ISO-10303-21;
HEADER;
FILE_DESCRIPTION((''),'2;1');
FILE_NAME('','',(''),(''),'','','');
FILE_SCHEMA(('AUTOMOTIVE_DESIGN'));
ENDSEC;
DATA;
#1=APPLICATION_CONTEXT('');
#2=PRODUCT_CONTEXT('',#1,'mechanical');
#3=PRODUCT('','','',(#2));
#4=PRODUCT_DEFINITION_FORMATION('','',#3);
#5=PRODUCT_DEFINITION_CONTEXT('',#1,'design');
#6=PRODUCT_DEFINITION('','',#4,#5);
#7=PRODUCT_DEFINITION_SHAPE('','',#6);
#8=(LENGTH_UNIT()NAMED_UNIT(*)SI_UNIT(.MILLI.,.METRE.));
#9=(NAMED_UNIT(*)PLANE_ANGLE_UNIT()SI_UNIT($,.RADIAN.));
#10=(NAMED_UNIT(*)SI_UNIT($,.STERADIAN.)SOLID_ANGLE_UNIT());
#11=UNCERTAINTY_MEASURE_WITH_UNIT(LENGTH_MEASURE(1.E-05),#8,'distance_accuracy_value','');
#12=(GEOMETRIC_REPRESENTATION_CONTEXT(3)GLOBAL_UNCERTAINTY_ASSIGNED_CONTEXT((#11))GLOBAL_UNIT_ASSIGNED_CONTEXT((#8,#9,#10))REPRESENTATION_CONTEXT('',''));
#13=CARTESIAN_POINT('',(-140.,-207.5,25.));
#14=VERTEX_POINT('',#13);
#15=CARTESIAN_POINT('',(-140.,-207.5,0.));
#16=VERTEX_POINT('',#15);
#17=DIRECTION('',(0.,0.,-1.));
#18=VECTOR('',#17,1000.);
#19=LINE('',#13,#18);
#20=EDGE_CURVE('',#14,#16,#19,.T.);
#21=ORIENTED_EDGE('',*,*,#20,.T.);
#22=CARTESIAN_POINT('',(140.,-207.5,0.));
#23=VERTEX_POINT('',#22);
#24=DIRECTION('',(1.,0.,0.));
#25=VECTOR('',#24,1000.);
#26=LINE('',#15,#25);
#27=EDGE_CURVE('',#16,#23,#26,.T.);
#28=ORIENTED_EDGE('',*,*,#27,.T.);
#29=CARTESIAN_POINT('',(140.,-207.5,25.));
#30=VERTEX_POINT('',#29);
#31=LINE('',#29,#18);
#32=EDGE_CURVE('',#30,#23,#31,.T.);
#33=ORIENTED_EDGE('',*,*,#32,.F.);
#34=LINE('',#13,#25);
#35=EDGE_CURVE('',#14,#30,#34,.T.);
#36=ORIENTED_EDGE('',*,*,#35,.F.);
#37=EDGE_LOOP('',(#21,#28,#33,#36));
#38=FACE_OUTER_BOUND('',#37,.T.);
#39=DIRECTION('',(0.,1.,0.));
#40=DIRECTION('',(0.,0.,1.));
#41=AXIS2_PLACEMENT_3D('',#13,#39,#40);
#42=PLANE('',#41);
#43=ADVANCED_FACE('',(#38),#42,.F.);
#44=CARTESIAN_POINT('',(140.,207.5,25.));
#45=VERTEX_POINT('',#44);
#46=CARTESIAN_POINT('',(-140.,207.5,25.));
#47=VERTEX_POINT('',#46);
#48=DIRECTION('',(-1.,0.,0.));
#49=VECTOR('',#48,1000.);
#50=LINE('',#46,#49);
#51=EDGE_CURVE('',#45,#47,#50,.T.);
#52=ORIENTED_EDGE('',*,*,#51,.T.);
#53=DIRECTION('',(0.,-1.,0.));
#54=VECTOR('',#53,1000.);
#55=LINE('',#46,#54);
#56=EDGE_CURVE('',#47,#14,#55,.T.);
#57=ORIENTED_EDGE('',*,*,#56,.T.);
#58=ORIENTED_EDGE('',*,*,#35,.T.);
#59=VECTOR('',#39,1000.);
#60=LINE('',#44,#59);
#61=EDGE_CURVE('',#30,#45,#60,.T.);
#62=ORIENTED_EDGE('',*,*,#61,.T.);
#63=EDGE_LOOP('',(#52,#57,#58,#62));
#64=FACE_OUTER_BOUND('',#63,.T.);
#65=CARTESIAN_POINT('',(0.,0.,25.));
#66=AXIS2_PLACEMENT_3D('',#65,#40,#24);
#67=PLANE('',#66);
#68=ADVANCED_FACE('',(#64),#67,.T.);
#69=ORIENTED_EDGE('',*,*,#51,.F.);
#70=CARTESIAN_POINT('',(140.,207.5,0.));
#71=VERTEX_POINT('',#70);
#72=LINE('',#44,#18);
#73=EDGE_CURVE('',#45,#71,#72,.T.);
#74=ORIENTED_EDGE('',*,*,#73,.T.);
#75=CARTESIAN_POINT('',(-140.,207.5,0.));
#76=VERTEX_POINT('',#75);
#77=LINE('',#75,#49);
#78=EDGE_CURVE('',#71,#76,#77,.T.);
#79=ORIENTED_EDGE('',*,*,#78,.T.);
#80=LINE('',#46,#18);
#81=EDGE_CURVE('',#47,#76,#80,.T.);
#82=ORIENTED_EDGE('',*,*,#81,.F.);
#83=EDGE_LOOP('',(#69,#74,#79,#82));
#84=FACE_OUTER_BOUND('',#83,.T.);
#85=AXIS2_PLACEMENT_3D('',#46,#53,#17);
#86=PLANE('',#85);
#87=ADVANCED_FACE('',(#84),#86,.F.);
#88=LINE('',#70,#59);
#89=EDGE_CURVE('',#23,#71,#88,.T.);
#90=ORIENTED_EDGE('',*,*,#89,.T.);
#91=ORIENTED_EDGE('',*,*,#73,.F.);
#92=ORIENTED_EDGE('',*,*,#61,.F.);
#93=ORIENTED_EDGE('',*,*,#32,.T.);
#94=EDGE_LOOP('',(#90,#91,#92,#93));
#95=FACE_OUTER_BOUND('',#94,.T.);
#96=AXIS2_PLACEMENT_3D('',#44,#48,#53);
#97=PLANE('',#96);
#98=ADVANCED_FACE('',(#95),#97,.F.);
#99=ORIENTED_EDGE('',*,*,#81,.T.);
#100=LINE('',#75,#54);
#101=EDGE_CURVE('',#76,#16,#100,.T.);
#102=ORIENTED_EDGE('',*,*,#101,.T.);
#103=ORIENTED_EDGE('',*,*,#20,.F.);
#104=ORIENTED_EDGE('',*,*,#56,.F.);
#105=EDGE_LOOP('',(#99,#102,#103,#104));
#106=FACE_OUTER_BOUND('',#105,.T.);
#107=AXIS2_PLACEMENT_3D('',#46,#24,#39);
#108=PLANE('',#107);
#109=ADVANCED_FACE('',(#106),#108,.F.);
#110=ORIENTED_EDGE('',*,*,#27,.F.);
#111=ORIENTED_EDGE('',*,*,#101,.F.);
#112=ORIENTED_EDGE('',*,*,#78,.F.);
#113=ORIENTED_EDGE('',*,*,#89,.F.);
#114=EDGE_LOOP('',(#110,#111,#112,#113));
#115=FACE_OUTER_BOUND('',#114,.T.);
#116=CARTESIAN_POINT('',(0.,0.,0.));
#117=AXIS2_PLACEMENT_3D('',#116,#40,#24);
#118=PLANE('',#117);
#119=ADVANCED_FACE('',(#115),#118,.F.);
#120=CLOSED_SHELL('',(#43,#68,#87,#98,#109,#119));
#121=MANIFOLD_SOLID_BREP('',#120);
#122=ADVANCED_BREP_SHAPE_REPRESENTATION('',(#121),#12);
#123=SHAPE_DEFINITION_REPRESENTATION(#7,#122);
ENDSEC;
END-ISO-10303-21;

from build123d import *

# Parameters (mm, degrees)
SKETCH1_W           = 280
SKETCH1_H           = 415
BOSS_EXTRUDE1_DEPTH = 25


with BuildPart() as part:
    # Sketch1 → Boss-Extrude1 (new body)
    with BuildSketch(Plane.XY):
        Rectangle(SKETCH1_W, SKETCH1_H)
    extrude(amount=BOSS_EXTRUDE1_DEPTH)


solid = part.part
